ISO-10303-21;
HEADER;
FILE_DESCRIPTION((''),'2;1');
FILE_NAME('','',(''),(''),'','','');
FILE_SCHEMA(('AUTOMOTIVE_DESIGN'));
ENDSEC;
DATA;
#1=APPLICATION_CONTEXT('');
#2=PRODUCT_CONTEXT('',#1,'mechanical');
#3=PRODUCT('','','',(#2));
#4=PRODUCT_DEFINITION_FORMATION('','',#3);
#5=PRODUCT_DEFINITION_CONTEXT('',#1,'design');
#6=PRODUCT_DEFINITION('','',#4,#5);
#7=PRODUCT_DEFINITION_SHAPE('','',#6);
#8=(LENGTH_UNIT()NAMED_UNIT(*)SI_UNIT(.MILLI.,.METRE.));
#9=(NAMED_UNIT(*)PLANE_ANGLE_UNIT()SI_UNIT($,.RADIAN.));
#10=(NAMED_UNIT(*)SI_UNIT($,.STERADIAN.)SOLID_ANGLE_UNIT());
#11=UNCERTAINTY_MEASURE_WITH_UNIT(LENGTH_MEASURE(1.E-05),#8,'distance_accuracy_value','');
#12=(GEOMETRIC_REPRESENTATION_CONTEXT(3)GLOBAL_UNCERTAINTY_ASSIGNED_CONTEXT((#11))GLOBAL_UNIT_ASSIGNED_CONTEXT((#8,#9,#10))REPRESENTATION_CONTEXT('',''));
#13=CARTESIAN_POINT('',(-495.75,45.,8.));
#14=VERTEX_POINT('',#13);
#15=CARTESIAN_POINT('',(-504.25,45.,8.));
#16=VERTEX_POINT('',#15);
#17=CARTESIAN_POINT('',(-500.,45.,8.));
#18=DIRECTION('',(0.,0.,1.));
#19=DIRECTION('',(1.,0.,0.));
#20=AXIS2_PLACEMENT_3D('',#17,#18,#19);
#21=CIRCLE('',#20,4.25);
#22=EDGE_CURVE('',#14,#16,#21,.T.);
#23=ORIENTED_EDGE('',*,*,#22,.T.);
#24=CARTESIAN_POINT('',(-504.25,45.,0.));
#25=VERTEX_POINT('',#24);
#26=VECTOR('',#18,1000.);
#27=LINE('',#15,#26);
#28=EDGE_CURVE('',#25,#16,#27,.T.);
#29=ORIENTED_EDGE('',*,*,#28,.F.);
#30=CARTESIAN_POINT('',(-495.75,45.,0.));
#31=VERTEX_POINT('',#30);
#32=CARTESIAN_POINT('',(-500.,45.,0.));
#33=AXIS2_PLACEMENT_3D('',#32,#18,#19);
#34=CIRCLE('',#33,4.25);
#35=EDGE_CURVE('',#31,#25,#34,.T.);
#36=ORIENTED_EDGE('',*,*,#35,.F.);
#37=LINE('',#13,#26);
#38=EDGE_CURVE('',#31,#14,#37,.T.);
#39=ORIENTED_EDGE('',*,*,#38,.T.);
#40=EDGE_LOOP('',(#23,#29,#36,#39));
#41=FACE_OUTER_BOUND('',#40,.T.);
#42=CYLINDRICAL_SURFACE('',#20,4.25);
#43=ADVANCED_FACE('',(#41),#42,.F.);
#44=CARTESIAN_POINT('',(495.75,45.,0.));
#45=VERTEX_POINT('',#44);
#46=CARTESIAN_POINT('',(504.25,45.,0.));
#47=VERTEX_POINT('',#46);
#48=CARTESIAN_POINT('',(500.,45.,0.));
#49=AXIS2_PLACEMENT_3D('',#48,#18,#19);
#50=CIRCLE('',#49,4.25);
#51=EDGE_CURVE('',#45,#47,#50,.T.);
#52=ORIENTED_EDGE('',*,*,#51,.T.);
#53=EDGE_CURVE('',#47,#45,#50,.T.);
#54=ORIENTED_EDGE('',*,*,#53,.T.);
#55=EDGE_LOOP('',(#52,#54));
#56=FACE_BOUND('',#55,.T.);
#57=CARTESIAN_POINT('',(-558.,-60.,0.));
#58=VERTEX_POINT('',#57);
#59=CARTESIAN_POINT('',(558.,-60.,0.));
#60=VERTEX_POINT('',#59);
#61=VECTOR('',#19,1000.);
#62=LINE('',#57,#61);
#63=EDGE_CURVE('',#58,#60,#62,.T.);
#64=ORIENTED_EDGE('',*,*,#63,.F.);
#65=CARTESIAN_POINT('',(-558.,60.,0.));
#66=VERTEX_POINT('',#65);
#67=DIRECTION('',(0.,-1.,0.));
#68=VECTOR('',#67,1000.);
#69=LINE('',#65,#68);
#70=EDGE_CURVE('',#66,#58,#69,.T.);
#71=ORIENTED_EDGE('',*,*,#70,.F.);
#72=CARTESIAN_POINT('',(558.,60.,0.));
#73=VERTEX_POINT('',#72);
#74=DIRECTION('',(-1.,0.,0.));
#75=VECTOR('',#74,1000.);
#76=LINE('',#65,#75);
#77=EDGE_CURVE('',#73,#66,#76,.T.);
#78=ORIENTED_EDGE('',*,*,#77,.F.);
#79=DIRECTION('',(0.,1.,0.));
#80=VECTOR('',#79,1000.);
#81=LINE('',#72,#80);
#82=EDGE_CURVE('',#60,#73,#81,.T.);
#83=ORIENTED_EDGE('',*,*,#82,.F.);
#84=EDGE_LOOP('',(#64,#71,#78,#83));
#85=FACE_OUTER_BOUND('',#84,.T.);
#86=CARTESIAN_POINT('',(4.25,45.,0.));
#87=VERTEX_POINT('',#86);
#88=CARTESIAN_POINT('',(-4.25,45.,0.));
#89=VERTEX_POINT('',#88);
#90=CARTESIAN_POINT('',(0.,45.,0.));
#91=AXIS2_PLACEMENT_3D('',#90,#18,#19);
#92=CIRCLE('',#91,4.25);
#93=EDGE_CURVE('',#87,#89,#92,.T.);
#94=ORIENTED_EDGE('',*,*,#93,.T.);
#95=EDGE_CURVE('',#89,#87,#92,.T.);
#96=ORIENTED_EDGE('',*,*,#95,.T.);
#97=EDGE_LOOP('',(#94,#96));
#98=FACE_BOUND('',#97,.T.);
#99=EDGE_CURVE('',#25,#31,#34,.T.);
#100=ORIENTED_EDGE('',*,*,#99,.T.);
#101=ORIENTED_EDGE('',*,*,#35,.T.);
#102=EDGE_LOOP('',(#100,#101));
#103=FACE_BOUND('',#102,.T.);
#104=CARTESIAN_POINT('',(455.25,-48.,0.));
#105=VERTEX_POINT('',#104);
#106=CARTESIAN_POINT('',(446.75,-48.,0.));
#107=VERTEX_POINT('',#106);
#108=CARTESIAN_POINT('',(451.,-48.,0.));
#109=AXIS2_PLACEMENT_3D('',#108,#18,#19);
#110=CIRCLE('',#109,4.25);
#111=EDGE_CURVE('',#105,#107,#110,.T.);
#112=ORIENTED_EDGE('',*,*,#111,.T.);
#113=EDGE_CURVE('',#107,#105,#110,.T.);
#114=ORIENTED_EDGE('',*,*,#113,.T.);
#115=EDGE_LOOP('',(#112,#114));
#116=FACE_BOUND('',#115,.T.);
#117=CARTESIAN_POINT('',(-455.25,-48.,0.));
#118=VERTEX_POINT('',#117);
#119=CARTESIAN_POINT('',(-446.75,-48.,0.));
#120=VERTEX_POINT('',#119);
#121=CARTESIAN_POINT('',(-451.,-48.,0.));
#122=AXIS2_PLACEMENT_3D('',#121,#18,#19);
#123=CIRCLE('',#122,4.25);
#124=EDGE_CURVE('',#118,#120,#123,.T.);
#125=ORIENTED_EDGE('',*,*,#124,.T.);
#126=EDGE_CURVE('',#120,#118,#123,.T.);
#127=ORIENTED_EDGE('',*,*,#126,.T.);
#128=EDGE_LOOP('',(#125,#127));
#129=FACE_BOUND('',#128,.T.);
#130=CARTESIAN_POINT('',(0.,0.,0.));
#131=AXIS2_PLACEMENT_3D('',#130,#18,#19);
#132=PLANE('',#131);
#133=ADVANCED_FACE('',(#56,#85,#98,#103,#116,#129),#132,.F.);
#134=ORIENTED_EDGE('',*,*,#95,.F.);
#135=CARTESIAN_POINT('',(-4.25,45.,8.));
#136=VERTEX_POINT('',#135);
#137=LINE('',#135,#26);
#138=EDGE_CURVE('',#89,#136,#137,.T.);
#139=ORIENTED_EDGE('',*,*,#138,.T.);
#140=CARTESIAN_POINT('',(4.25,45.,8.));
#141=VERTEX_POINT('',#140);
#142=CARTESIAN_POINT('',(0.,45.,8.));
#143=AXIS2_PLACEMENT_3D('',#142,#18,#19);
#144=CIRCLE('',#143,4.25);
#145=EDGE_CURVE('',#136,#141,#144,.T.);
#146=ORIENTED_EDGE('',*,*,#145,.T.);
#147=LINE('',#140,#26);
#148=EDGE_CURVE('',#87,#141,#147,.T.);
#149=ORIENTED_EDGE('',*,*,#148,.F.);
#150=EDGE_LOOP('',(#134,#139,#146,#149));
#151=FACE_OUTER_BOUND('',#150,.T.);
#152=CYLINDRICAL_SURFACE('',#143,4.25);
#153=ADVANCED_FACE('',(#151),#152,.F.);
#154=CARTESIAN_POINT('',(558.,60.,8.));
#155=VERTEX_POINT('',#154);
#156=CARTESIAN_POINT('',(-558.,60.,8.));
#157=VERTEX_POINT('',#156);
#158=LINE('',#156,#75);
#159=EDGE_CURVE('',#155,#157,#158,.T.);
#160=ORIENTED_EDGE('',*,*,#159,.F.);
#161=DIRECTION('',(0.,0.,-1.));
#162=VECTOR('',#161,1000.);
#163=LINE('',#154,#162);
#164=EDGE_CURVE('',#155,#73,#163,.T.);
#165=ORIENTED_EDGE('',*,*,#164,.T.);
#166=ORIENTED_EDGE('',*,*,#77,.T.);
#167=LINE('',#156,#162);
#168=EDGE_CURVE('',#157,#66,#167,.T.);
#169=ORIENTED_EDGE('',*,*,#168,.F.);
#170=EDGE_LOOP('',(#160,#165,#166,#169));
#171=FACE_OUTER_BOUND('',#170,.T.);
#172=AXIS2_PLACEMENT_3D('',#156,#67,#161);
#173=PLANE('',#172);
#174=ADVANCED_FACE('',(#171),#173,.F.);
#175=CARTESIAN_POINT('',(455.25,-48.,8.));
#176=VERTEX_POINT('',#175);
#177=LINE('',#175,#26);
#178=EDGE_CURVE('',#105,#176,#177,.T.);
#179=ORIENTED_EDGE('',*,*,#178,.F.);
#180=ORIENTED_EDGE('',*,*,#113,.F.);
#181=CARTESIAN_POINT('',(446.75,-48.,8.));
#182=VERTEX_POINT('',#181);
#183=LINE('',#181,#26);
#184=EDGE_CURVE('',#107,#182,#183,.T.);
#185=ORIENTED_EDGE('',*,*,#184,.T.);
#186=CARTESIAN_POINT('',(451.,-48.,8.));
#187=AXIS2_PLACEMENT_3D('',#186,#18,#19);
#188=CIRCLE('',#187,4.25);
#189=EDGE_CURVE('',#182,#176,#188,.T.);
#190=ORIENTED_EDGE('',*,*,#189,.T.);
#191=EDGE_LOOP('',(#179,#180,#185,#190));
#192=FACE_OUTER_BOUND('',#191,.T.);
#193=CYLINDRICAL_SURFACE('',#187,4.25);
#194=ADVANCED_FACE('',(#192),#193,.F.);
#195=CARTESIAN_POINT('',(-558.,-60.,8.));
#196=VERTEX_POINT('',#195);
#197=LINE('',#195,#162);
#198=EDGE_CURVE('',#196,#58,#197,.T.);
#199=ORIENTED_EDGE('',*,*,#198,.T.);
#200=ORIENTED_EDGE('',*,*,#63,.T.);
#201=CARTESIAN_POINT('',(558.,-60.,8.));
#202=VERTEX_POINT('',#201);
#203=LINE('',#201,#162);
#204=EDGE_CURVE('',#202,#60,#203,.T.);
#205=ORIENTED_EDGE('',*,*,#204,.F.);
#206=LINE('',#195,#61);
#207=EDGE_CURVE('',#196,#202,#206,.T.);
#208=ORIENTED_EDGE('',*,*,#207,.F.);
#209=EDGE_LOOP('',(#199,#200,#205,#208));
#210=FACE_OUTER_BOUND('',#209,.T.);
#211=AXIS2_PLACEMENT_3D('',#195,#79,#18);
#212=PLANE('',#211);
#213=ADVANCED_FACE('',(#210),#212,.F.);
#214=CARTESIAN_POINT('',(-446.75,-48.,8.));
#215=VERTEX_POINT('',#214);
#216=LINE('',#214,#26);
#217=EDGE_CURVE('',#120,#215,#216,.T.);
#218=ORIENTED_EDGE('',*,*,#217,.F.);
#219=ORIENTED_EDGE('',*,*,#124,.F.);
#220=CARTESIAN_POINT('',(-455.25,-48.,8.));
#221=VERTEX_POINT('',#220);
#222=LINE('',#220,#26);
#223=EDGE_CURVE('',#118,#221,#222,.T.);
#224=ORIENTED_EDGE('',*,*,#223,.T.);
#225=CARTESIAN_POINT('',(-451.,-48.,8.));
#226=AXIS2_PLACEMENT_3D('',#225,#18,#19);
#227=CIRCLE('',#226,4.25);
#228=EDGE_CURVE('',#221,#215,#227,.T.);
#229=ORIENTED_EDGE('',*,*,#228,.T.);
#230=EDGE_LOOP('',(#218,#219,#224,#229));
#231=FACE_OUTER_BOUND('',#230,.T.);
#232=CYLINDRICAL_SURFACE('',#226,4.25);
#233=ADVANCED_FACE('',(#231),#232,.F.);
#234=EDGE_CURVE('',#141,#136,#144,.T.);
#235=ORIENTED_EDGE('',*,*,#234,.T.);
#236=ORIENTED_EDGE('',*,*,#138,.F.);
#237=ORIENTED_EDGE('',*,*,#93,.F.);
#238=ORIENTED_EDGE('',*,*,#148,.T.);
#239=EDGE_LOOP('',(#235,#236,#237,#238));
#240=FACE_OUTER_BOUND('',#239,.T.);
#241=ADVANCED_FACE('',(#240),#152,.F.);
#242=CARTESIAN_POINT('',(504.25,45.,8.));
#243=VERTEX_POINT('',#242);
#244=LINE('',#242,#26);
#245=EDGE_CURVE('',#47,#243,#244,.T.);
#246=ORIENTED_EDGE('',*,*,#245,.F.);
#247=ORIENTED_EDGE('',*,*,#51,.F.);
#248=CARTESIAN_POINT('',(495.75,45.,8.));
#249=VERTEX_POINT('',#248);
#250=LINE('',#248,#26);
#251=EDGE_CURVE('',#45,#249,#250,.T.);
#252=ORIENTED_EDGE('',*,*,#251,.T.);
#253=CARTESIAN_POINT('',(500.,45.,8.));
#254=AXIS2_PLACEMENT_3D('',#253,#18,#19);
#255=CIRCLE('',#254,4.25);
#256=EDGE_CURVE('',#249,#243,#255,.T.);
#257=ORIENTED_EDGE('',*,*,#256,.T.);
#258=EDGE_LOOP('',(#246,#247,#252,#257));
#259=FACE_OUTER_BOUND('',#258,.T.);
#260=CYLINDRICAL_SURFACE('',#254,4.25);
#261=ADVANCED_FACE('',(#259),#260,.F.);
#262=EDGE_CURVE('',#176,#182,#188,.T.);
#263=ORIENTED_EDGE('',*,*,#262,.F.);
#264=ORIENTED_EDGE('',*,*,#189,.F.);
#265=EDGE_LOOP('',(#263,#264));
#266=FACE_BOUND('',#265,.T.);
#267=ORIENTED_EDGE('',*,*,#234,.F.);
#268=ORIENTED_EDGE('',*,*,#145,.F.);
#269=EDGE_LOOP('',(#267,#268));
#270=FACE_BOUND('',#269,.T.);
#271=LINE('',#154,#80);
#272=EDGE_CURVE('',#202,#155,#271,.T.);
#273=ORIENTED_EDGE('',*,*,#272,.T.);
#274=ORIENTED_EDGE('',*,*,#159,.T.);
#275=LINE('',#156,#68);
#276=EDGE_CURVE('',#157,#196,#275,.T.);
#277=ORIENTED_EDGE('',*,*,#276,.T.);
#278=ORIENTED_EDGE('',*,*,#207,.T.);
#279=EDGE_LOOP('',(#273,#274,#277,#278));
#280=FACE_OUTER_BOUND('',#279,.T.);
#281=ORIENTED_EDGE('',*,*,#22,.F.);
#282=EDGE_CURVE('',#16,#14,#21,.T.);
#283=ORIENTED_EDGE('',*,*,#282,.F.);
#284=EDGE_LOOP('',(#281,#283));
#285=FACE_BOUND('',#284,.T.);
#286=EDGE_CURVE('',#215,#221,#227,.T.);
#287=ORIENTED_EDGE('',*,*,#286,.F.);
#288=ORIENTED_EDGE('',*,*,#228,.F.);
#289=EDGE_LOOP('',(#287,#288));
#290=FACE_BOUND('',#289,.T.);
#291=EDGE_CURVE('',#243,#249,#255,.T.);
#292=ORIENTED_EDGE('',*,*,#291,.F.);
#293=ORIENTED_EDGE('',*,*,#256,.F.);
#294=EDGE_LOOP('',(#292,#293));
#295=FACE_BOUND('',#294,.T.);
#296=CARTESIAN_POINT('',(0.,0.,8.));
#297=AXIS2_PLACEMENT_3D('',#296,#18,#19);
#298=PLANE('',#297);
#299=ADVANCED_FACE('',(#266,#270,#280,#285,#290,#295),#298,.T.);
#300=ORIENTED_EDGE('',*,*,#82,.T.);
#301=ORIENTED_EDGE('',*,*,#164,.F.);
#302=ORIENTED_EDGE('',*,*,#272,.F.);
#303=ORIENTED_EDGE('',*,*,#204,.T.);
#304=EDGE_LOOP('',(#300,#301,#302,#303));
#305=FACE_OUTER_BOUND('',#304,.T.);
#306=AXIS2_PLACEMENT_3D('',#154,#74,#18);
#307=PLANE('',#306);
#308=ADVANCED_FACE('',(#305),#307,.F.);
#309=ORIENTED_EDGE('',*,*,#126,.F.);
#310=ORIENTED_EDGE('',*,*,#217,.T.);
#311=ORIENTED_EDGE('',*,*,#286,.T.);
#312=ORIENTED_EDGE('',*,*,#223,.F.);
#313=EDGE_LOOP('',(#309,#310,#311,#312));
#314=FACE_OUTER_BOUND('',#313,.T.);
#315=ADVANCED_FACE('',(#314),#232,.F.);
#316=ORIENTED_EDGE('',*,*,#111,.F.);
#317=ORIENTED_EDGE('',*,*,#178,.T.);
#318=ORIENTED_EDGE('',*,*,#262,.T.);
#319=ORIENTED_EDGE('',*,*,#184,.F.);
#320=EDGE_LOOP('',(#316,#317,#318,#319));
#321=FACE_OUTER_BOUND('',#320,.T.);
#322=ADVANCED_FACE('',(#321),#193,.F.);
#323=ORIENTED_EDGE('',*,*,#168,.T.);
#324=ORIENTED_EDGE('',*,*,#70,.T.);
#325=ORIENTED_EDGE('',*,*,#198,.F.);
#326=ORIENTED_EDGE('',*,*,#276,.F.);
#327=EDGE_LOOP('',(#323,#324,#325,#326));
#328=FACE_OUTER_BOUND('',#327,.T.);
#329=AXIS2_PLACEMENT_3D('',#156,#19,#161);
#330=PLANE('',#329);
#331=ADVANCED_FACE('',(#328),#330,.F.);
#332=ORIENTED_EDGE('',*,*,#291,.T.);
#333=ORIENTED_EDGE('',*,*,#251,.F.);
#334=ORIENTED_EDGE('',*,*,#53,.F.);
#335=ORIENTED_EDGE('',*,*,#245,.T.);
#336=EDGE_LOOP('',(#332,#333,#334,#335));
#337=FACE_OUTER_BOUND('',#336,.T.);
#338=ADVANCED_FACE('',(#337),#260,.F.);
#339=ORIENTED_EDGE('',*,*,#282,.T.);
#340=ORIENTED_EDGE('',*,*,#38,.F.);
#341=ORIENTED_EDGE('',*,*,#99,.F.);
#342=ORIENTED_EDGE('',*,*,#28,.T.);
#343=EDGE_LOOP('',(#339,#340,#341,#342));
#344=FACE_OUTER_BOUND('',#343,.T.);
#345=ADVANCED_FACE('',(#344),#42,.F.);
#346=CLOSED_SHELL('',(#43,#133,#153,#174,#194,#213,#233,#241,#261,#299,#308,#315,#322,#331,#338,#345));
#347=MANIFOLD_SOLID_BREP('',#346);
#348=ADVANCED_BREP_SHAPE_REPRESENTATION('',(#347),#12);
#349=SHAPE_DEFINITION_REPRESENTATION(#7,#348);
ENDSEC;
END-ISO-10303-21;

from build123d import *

# Parameters (mm, degrees)
SKETCH1_W              = 1116
SKETCH1_H              = 120
BOSS_EXTRUDE1_DEPTH    = 8
M10_TAPPED_HOLE1_D     = 8.5
M10_TAPPED_HOLE1_DEPTH = 24.5
M10_TAPPED_HOLE1_TIP   = 2.553657631


with BuildPart() as part:
    # Sketch1 → Boss-Extrude1 (new body)
    with BuildSketch(Plane.XY):
        Rectangle(SKETCH1_W, SKETCH1_H)
    extrude(amount=BOSS_EXTRUDE1_DEPTH)

    # M10 Tapped Hole1
    with Locations(Plane.XY.offset(8)):
        with Locations((-500, 45), (-451, -48), (0, 45), (500, 45), (451, -48)):
            Hole(M10_TAPPED_HOLE1_D / 2, depth=M10_TAPPED_HOLE1_DEPTH)
            with Locations((0, 0, -(M10_TAPPED_HOLE1_DEPTH + M10_TAPPED_HOLE1_TIP / 2))):  # 118° drill point
                Cone(0, M10_TAPPED_HOLE1_D / 2, M10_TAPPED_HOLE1_TIP, mode=Mode.SUBTRACT)


solid = part.part
